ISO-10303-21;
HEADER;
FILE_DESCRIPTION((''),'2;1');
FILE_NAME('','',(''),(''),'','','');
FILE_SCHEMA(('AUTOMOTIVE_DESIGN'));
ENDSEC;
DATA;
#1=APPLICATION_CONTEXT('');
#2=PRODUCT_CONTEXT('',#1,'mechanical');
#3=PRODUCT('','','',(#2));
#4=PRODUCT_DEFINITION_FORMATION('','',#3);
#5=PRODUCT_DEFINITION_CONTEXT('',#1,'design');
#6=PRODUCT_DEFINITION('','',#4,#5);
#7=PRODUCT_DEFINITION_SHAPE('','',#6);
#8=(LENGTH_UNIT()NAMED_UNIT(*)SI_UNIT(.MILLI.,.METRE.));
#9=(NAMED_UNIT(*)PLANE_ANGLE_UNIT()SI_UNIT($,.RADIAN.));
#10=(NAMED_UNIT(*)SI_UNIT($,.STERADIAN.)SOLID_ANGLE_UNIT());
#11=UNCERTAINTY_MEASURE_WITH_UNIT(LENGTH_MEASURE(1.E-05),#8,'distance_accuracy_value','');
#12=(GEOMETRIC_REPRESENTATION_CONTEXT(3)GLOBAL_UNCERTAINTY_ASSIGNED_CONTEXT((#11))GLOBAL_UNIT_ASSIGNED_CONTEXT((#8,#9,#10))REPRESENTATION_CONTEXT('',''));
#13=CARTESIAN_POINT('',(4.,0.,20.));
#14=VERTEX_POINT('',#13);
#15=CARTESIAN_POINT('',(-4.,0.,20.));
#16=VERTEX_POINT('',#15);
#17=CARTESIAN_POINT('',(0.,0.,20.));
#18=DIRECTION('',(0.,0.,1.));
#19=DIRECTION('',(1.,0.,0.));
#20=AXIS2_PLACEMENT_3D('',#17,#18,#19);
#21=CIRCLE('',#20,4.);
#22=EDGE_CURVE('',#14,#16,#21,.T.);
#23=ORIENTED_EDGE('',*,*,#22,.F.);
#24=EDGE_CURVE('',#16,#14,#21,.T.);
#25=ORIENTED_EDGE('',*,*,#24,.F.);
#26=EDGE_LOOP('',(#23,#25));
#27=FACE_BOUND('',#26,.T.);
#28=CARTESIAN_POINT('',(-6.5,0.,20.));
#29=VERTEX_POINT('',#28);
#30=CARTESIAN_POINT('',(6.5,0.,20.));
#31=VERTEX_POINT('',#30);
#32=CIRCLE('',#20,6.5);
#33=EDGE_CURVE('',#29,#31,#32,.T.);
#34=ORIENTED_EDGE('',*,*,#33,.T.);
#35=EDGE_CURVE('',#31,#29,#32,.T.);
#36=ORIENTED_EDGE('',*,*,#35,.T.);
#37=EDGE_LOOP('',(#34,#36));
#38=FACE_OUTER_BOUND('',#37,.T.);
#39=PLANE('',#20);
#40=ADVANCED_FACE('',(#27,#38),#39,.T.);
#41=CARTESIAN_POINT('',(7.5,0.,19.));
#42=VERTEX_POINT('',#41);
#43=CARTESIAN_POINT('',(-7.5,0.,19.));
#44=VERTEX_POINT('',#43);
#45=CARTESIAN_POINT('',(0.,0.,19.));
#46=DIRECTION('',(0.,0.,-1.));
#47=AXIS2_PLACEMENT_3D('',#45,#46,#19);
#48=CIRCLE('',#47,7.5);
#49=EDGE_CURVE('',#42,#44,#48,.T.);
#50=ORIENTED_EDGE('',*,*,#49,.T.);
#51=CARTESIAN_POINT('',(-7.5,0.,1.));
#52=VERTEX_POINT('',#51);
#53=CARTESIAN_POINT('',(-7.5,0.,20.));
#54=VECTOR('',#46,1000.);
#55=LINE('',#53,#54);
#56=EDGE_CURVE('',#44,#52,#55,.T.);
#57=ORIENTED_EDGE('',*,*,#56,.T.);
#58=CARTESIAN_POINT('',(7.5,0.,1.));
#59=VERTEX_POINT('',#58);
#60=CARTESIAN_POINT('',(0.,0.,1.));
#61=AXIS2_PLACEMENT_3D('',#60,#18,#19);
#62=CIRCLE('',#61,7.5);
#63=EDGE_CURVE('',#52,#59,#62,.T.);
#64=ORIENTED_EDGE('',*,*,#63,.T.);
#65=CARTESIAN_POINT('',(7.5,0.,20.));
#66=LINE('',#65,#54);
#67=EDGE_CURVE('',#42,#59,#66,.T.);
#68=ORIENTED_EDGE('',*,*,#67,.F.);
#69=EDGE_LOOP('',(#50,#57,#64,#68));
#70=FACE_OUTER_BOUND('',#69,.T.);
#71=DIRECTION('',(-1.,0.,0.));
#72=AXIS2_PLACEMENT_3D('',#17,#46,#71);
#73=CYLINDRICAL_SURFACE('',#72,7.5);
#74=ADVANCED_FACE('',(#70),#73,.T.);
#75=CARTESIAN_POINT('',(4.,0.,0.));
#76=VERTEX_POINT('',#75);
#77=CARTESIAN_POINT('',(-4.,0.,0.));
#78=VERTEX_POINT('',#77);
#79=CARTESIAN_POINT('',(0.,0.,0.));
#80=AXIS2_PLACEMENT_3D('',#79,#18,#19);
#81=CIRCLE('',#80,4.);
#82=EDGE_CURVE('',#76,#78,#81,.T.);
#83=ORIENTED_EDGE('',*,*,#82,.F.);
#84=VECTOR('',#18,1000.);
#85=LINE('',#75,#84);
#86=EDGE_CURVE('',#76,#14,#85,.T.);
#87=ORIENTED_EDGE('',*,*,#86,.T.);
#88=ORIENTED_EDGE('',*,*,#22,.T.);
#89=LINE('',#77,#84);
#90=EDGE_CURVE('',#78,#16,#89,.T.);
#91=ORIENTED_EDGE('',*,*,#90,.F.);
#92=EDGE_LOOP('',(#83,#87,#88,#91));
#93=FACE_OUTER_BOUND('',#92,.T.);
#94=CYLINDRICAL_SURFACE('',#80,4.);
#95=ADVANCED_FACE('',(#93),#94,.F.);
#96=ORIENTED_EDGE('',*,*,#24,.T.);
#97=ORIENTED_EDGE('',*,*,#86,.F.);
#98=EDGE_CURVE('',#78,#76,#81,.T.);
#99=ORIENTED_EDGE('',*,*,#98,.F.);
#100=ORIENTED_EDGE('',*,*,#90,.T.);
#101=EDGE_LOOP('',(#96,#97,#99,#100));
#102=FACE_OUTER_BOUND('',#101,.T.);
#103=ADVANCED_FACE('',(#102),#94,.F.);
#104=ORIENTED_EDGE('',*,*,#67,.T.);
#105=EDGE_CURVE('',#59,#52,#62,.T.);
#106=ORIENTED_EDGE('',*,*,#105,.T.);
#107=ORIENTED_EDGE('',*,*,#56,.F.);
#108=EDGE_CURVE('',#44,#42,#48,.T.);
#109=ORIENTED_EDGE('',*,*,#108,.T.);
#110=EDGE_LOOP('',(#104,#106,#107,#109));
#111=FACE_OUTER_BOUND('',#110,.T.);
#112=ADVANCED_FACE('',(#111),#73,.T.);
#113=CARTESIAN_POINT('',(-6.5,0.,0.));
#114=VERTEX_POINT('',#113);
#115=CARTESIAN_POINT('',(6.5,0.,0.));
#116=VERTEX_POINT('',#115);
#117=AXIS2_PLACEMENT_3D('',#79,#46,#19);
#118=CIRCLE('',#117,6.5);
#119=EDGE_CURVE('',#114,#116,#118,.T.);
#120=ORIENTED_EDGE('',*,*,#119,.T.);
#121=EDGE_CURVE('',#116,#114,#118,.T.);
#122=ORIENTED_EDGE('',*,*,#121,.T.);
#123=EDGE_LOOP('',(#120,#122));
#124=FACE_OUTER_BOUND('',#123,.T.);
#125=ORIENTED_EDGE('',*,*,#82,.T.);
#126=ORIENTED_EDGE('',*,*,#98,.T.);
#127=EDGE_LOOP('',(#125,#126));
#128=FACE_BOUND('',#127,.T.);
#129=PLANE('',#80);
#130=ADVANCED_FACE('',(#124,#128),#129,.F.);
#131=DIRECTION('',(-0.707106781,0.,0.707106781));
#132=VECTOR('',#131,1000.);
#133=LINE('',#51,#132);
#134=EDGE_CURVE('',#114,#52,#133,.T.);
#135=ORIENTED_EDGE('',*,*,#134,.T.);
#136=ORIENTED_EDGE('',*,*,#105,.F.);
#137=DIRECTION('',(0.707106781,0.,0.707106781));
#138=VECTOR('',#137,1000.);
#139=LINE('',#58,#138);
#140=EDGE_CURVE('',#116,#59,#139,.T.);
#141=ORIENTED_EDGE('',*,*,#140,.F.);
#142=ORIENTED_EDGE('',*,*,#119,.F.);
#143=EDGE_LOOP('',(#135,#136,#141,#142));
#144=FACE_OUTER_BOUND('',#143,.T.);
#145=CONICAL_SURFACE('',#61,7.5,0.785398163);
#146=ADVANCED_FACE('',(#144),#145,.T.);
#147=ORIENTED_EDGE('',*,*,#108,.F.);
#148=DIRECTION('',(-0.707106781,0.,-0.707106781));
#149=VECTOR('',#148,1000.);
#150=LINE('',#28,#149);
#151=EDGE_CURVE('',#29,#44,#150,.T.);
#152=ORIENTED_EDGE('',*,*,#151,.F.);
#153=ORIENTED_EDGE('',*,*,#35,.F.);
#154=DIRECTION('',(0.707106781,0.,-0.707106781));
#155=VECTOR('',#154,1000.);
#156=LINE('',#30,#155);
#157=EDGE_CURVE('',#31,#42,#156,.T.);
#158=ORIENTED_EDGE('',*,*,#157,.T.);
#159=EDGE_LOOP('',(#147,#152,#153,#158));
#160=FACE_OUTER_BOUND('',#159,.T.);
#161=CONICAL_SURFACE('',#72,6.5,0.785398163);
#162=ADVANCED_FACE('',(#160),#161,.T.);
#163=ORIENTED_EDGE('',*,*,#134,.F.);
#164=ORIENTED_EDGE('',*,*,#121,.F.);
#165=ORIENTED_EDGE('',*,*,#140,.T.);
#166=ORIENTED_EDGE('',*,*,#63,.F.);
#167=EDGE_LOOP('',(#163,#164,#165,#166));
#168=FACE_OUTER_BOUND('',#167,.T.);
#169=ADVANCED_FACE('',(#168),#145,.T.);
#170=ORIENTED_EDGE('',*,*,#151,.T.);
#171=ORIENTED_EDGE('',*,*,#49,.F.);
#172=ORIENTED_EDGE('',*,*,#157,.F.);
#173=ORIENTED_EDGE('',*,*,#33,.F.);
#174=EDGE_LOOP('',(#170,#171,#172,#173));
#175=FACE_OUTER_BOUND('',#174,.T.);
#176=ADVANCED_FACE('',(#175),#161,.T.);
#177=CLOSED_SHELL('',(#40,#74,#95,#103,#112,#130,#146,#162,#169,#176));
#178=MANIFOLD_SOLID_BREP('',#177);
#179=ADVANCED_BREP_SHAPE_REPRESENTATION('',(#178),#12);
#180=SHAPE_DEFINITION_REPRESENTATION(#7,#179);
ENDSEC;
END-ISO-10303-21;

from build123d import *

# Parameters (mm, degrees)
SKETCH1_R           = 7.5
BOSS_EXTRUDE1_DEPTH = 20
CHAMFER1_SIZE       = 1
SKETCH2_R           = 4
CUT_EXTRUDE1_DEPTH  = 20


with BuildPart() as part:
    # Sketch1 → Boss-Extrude1 (new body)
    with BuildSketch(Plane.XY):
        Circle(SKETCH1_R)
    extrude(amount=BOSS_EXTRUDE1_DEPTH)

    # Chamfer1
    chamfer1_edges = [part.edges().sort_by_distance(p)[0] for p in [
        (-7.5, 0, 0),
        (-7.5, 0, 20),
    ]]
    chamfer(chamfer1_edges, length=CHAMFER1_SIZE)

    # Sketch2 → Cut-Extrude1 (cut)
    with BuildSketch(Plane.XY.offset(20)):
        Circle(SKETCH2_R)
    extrude(amount=-CUT_EXTRUDE1_DEPTH, mode=Mode.SUBTRACT)


solid = part.part
